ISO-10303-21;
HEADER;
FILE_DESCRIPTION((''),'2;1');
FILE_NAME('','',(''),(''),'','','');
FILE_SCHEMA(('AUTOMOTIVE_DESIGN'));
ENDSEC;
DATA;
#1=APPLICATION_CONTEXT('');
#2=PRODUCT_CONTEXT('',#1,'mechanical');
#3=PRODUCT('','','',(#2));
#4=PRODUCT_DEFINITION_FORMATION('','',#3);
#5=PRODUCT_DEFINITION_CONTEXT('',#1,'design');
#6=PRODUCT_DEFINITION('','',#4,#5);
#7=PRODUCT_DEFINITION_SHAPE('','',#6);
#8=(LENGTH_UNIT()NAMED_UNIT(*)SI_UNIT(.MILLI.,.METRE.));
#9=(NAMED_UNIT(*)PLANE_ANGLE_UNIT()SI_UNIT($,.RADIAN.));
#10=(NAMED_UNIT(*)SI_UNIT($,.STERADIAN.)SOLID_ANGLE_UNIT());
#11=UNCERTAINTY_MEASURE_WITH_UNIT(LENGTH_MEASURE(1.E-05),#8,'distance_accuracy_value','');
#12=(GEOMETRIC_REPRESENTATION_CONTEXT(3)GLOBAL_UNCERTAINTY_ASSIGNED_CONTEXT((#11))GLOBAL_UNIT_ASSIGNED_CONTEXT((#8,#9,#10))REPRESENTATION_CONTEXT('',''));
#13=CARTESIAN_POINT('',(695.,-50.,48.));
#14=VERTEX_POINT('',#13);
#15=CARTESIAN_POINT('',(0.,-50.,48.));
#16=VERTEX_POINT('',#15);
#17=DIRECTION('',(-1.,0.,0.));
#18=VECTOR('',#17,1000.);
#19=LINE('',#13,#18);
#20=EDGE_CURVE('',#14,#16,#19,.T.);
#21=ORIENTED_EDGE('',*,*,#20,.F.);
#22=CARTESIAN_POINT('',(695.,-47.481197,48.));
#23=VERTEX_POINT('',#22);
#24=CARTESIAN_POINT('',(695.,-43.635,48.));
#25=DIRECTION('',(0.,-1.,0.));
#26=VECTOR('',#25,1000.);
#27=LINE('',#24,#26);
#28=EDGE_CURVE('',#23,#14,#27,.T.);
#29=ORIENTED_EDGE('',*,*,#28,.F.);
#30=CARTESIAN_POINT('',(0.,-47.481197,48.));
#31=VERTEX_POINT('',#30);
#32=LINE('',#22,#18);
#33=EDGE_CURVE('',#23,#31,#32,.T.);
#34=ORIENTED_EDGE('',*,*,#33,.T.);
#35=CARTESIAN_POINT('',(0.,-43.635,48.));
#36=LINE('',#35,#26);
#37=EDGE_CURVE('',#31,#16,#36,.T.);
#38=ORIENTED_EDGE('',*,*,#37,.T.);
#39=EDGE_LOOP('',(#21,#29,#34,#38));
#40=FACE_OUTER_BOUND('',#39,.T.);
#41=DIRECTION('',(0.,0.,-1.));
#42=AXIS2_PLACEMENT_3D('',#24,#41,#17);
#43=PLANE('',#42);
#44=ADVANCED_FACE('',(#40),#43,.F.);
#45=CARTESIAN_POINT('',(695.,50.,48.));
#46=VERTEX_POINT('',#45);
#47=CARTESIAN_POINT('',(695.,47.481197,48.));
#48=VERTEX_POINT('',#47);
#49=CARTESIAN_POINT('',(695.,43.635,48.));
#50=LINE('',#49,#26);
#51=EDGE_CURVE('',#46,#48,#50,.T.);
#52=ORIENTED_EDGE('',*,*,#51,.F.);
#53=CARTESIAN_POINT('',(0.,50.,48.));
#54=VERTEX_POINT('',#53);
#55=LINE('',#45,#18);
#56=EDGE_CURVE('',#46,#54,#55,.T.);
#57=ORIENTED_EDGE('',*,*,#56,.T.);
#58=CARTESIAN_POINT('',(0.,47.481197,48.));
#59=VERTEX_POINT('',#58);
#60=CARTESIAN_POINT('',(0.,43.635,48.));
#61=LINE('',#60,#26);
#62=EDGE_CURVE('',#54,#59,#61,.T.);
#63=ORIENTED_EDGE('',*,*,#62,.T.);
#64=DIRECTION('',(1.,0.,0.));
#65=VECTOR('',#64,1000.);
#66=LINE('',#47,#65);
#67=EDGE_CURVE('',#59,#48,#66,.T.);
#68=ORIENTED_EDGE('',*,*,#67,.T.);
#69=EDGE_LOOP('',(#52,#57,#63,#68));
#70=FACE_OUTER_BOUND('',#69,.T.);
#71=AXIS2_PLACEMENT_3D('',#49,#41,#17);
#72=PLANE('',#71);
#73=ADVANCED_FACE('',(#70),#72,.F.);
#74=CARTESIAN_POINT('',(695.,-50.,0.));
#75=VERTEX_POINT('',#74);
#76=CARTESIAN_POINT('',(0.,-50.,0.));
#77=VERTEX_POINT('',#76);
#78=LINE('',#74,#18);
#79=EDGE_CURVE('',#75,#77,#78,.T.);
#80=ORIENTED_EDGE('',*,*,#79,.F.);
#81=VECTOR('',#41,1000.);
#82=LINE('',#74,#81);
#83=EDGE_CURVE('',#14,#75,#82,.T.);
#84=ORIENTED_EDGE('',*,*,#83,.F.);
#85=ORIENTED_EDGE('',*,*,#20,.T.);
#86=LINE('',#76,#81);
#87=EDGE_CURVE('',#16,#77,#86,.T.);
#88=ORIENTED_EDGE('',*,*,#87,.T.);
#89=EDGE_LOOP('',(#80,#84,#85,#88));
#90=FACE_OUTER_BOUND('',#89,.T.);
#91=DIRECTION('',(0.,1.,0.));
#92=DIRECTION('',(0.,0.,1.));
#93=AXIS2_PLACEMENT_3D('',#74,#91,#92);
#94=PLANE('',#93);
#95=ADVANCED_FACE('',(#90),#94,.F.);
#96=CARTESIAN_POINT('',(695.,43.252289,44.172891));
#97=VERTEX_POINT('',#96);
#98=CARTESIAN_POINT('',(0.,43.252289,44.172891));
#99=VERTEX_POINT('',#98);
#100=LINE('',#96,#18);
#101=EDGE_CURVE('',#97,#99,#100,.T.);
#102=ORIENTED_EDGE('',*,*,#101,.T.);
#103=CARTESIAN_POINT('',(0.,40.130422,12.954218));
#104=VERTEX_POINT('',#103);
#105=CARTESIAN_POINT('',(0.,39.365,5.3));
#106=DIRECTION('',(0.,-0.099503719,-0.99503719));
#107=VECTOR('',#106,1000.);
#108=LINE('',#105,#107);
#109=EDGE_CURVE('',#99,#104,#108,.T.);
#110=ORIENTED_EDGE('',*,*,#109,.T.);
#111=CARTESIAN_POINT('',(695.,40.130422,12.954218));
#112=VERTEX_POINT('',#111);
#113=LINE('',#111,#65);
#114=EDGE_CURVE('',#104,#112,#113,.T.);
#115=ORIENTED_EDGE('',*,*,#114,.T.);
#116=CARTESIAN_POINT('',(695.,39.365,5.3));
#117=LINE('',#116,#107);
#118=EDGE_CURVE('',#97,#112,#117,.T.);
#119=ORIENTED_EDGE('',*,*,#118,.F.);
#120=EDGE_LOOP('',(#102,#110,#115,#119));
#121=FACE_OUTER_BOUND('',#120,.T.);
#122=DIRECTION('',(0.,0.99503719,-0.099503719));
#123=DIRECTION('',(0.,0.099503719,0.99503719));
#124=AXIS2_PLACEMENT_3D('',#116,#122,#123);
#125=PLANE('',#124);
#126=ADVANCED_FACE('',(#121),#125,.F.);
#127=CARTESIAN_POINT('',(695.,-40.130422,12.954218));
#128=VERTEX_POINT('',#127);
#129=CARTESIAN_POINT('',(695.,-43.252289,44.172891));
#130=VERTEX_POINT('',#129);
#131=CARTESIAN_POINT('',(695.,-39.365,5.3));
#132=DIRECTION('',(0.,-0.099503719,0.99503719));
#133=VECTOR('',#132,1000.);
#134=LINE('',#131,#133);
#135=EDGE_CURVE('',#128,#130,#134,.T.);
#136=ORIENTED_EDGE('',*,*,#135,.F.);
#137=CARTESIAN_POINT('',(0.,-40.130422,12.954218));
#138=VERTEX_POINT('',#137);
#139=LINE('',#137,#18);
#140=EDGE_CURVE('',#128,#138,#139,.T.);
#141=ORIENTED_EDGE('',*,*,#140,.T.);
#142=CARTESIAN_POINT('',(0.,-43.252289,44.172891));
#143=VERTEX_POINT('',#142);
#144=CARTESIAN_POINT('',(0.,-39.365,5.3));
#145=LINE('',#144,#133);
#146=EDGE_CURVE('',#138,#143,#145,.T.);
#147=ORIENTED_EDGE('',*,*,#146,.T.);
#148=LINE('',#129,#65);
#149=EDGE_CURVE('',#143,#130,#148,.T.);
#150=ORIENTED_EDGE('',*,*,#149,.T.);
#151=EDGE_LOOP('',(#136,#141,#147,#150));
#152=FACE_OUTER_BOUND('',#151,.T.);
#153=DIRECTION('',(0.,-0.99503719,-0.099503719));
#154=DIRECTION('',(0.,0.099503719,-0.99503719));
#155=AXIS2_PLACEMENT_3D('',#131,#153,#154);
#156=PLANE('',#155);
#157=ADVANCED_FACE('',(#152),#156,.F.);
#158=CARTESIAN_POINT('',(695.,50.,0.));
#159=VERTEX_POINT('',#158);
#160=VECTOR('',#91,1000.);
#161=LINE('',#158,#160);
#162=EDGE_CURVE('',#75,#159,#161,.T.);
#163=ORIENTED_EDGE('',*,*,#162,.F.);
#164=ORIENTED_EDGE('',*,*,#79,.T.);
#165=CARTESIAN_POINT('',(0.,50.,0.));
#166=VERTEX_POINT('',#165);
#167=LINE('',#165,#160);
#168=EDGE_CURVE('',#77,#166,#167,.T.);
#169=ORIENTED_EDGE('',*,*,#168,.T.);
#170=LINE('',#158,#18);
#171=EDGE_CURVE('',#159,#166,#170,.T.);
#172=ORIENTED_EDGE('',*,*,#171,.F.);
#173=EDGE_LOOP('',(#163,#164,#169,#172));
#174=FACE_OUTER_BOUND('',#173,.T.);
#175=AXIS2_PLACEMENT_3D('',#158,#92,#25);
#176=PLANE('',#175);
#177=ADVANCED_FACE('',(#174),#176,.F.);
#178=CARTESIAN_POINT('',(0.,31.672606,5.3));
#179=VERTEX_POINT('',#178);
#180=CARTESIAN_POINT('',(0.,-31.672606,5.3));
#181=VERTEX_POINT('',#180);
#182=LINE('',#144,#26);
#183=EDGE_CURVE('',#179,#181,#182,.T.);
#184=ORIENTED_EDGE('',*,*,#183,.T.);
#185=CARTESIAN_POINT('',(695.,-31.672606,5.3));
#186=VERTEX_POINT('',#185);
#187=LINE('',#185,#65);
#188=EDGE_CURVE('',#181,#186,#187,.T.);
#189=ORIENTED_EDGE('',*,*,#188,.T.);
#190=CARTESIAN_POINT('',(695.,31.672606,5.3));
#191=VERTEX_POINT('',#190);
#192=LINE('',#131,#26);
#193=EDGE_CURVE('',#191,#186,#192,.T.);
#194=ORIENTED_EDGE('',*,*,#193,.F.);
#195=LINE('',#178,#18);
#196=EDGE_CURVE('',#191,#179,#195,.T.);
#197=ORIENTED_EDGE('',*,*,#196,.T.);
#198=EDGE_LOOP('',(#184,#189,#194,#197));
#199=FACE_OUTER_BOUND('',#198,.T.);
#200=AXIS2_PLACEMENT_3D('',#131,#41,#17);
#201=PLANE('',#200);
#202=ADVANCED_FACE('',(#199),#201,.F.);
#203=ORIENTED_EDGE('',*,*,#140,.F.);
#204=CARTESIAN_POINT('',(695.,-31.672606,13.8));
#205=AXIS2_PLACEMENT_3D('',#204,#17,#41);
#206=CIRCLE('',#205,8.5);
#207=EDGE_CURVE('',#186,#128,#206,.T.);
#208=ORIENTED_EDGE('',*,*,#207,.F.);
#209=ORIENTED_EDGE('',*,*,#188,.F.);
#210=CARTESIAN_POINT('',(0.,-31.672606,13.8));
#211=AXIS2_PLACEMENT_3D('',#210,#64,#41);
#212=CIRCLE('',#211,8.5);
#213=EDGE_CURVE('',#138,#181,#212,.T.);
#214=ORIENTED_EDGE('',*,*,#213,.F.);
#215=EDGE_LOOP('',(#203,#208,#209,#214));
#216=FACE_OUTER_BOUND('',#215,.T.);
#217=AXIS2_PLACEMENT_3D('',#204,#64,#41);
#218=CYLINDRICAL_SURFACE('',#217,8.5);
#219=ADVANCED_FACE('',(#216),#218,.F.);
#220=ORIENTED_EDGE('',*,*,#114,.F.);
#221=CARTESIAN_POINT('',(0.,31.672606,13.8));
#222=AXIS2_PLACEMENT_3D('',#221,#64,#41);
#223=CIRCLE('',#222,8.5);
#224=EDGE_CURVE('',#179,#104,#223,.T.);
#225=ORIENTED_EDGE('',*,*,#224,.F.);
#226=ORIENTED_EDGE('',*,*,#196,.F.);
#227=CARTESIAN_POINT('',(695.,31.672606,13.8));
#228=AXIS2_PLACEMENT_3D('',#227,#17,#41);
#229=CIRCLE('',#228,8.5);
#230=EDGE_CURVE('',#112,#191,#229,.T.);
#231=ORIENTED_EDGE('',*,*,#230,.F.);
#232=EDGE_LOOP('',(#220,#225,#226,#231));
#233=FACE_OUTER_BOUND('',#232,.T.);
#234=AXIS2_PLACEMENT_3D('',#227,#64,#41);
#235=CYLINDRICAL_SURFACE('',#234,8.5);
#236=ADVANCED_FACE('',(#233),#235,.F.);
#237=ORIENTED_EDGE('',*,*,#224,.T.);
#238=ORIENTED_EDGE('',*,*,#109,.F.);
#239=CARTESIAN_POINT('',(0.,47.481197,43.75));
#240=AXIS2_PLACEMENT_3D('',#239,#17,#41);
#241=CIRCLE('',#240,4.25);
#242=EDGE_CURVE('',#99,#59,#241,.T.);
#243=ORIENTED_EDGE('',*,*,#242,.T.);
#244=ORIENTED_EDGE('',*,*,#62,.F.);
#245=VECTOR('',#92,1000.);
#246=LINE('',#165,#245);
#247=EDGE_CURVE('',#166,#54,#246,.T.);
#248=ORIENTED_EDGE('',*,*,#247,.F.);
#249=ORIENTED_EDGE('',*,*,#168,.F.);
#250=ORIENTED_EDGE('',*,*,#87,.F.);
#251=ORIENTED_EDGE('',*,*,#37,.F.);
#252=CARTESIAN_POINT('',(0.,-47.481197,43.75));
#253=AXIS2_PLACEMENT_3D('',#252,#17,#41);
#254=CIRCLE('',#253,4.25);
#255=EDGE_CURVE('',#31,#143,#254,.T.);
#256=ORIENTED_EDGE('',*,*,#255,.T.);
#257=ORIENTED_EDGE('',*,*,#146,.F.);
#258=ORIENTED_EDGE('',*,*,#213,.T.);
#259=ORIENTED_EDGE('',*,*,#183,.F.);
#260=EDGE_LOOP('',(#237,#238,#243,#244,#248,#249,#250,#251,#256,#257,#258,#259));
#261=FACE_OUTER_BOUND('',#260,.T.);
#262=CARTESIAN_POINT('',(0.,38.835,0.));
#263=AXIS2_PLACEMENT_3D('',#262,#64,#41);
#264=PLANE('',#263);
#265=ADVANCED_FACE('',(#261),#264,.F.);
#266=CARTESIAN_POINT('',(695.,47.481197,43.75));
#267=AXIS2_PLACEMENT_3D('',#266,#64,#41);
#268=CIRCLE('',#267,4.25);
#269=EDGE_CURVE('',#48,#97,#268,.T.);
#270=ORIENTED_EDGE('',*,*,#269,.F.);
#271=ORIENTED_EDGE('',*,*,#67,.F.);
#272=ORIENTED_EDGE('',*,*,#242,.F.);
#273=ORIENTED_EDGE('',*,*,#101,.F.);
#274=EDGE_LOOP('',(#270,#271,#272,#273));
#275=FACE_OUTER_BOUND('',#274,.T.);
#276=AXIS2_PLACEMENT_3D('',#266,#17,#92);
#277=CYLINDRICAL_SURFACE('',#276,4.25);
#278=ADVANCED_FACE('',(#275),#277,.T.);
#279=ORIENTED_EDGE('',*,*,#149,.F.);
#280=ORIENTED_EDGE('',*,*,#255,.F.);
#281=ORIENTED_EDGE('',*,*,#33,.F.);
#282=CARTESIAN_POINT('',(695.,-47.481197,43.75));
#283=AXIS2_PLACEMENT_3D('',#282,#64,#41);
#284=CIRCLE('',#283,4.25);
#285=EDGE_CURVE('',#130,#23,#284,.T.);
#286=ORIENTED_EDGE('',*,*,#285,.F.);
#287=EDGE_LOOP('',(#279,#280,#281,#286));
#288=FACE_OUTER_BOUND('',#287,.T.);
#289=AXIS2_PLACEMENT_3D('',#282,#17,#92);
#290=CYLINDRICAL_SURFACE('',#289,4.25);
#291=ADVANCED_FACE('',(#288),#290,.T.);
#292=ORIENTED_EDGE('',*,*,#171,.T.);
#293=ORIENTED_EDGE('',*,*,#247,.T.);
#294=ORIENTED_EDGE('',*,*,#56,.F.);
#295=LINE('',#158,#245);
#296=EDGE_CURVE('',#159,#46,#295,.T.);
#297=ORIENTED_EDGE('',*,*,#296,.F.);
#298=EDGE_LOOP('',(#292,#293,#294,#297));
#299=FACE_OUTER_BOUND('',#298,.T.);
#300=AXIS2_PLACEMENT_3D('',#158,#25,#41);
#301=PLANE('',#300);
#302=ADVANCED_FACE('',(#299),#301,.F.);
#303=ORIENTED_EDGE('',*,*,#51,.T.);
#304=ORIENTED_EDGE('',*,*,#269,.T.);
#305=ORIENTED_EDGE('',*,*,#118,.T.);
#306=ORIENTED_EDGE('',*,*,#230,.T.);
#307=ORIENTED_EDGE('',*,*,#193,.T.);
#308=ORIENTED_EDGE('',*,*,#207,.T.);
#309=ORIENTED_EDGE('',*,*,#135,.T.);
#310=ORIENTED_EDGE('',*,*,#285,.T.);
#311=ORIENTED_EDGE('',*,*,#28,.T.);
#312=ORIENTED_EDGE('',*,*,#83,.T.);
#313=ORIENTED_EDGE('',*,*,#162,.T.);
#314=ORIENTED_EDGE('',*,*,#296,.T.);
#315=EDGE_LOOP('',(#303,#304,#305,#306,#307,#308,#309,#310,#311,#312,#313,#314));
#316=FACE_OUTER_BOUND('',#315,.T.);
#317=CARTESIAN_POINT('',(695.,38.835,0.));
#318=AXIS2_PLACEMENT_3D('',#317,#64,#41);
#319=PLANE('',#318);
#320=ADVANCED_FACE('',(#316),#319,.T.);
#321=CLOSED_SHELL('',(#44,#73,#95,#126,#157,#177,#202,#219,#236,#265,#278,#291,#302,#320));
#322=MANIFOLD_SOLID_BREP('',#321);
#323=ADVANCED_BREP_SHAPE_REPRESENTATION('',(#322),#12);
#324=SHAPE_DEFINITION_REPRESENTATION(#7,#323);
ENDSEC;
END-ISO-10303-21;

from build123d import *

# Parameters (mm, degrees)
BASE_DEPTH = 695
FILLET1_R  = 8.5
FILLET2_R  = 4.25


with BuildPart() as part:
    # Sketch1 → Base (new body)
    with BuildSketch(Plane(origin=(0, 0, -28.211262136), x_dir=(0, 0, 1), z_dir=(1, 0, 0))):
        Polygon((28.211262136, -50), (28.211262136, 50), (76.211262136, 50), (76.211262136, 43.635), (33.511262136, 39.365), (33.511262136, -39.365), (76.211262136, -43.635), (76.211262136, -50), align=None)
    extrude(amount=BASE_DEPTH)

    # Fillet1
    fillet1_edges = [part.edges().sort_by_distance(p)[0] for p in [
        (347.5, -39.365, 5.3),
        (347.5, 39.365, 5.3),
    ]]
    fillet(fillet1_edges, radius=FILLET1_R)

    # Fillet2
    fillet2_edges = [part.edges().sort_by_distance(p)[0] for p in [
        (347.5, 43.635, 48),
        (347.5, -43.635, 48),
    ]]
    fillet(fillet2_edges, radius=FILLET2_R)


solid = part.part
